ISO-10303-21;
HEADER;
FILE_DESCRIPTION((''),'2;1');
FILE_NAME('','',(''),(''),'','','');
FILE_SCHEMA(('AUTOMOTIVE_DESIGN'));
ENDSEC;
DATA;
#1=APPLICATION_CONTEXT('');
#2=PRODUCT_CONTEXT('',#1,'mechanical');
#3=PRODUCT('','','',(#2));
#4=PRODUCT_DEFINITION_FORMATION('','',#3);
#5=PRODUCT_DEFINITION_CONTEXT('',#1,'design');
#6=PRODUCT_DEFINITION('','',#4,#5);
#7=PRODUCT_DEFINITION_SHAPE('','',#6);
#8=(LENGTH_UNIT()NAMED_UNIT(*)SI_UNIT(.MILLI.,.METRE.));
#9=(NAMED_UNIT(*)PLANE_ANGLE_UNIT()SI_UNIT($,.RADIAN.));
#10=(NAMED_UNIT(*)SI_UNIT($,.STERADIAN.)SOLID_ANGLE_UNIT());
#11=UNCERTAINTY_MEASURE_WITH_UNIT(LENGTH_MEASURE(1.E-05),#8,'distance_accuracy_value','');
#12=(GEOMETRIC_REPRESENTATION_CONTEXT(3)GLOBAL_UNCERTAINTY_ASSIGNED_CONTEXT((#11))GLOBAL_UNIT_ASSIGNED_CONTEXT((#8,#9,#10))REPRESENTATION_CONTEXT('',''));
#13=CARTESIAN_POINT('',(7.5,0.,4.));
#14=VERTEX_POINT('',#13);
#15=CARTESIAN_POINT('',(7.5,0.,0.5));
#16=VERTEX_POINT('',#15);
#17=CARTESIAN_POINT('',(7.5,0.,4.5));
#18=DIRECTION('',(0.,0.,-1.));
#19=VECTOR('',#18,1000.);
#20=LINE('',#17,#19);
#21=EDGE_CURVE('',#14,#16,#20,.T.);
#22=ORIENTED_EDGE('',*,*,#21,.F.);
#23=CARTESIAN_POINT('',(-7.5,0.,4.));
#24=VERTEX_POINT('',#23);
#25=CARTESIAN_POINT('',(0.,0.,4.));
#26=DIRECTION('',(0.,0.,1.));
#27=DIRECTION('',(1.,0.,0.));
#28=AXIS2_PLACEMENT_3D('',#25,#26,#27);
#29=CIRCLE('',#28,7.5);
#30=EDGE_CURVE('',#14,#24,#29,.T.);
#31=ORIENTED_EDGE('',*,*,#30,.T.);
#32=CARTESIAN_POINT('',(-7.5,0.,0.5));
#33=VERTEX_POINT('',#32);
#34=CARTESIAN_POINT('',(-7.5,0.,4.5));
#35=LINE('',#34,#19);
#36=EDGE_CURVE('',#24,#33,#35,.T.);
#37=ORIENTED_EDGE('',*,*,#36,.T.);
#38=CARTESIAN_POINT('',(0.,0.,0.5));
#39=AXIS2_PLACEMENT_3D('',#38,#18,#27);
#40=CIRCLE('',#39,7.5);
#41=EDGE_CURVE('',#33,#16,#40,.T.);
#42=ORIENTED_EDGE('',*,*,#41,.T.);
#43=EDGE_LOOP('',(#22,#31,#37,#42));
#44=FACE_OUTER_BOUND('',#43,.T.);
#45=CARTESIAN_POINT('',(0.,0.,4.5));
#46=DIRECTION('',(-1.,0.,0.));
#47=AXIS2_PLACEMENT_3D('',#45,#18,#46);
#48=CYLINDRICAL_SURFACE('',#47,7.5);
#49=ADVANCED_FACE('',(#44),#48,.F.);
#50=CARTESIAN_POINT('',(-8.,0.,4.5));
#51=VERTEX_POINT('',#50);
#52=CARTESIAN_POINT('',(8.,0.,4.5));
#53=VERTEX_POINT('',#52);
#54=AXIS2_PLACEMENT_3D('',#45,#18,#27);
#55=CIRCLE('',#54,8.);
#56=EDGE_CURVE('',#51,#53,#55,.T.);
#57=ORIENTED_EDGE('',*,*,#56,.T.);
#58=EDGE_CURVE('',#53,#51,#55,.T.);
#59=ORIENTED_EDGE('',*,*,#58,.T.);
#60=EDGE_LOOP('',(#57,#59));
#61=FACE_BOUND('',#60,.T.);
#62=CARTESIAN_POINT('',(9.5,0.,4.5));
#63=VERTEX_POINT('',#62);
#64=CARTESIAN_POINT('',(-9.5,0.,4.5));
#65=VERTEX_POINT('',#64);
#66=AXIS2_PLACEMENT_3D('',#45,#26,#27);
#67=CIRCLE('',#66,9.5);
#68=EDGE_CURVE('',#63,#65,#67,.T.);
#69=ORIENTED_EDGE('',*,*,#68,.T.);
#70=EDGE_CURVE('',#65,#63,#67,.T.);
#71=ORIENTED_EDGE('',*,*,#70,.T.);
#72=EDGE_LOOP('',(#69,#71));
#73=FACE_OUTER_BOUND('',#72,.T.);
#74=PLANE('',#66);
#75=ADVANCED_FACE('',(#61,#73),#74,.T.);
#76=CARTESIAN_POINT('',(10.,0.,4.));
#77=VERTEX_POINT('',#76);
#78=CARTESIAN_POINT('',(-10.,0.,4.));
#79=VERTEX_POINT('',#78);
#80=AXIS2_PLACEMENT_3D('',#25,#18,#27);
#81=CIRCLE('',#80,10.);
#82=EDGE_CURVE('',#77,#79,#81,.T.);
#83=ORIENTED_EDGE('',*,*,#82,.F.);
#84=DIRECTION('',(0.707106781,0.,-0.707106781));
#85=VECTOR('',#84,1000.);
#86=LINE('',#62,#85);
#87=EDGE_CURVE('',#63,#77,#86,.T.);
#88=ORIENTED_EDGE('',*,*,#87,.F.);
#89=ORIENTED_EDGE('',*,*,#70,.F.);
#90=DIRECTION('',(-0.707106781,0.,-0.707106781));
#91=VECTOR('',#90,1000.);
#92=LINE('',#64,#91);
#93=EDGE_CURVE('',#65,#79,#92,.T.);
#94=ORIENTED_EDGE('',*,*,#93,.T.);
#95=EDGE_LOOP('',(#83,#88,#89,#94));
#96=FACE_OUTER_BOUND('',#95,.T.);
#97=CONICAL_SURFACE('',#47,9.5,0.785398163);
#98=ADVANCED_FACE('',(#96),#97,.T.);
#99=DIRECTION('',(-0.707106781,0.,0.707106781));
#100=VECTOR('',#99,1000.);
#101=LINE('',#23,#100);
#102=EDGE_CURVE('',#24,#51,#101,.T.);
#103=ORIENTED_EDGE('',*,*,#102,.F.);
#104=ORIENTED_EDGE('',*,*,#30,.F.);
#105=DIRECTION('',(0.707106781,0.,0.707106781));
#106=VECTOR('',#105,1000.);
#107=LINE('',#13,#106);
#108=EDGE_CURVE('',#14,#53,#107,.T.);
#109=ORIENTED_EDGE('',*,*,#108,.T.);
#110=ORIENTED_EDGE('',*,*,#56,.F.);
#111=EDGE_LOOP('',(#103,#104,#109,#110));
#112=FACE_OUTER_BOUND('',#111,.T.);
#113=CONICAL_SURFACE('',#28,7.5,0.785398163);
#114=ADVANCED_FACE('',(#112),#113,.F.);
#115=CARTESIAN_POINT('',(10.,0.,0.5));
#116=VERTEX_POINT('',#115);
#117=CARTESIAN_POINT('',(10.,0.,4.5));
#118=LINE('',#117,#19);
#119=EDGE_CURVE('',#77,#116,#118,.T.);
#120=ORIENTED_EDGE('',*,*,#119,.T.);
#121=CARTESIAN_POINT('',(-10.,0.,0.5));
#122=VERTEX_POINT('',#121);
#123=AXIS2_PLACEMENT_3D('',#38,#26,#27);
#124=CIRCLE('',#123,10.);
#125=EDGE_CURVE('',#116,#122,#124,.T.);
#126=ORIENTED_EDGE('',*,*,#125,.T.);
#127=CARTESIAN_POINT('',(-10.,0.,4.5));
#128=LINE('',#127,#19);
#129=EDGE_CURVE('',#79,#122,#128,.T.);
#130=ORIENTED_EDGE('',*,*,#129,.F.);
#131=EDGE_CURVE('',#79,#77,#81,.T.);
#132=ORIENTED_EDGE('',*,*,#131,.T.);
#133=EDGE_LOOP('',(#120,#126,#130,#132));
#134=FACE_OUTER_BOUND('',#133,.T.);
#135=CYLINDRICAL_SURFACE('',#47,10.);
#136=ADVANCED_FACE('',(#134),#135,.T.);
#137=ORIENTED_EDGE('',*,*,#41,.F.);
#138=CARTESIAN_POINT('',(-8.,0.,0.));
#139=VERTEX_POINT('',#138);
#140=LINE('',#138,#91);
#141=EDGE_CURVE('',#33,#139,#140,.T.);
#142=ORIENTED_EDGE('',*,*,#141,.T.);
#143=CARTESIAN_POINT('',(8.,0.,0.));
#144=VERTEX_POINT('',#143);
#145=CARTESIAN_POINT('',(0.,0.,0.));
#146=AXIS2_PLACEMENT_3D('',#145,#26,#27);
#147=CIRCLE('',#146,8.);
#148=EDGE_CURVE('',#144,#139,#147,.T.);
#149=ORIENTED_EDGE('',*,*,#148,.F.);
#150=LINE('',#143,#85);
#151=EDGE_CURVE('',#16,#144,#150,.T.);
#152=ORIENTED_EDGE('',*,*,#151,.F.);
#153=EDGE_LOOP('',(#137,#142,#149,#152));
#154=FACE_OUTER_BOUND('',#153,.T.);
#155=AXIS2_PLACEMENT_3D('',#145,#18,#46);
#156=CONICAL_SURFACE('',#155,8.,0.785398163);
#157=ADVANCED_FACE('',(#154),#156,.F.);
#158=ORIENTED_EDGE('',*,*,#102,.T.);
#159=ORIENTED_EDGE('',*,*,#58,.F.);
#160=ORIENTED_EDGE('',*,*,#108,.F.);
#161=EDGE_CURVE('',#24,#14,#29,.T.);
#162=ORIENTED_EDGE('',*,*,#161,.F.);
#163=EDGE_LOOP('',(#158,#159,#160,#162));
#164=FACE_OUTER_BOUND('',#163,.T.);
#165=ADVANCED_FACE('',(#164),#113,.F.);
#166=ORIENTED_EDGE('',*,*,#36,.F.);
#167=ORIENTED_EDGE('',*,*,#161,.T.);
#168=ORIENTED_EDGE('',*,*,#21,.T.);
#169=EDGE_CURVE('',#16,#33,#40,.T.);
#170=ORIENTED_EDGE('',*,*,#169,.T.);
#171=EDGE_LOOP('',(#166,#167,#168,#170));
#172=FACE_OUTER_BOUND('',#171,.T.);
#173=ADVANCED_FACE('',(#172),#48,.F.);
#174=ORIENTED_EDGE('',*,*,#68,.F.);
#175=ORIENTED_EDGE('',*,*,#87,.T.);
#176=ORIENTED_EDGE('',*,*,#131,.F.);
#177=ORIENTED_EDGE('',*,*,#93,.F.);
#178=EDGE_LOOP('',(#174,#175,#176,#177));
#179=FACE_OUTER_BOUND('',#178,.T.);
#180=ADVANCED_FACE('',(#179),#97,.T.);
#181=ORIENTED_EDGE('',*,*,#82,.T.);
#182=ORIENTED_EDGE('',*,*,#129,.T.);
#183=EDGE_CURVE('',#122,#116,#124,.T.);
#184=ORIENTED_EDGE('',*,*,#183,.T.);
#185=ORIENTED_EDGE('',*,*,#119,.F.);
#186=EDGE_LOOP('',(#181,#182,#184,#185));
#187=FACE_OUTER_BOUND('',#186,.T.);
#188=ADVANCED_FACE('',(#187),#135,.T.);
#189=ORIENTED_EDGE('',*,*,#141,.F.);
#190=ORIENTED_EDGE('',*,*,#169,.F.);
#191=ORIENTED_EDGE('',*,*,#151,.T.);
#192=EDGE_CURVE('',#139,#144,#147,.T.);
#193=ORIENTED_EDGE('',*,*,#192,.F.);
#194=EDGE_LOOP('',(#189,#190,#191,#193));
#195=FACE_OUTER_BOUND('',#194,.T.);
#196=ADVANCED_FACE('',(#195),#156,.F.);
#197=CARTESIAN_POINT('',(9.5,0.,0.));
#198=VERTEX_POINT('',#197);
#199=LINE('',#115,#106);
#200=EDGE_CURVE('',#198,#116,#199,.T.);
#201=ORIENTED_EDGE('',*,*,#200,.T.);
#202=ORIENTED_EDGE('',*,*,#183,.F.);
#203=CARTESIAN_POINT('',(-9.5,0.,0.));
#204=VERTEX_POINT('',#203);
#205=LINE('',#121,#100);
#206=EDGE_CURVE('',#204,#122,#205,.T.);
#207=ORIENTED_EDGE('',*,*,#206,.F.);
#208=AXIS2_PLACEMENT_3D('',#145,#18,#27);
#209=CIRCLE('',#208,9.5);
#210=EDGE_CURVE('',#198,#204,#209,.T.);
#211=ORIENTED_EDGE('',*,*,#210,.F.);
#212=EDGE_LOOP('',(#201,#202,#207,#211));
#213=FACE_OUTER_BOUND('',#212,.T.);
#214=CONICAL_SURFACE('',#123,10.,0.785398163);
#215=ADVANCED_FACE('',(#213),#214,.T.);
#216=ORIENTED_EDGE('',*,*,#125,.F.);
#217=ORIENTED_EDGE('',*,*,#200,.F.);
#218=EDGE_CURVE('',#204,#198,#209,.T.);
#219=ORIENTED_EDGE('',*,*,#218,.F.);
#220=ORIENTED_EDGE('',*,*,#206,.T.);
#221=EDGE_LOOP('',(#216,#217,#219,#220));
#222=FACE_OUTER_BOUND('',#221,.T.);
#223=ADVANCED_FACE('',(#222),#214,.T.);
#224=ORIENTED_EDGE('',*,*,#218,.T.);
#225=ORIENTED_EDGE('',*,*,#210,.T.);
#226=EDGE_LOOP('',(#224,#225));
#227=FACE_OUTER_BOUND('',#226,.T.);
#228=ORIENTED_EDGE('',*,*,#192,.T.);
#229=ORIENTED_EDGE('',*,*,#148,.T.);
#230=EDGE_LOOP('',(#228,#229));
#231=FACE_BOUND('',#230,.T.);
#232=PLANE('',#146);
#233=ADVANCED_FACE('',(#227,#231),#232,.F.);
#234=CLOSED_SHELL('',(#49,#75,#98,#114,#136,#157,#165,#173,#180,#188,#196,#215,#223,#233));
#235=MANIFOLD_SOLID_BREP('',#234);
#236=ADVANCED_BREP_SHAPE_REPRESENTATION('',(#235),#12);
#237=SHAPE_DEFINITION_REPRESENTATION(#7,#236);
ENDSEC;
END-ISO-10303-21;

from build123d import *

# Parameters (mm, degrees)
SKETCH1_R           = 10
SKETCH1_R_2         = 7.5
BOSS_EXTRUDE1_DEPTH = 4.5
CHAMFER1_SIZE       = 0.5


with BuildPart() as part:
    # Sketch1 → Boss-Extrude1 (new body)
    with BuildSketch(Plane.XY):
        Circle(SKETCH1_R)
        Circle(SKETCH1_R_2, mode=Mode.SUBTRACT)
    extrude(amount=BOSS_EXTRUDE1_DEPTH)

    # Chamfer1
    chamfer1_edges = [part.edges().sort_by_distance(p)[0] for p in [
        (-10, 0, 0),
        (-10, 0, 4.5),
        (-7.5, 0, 0),
        (-7.5, 0, 4.5),
    ]]
    chamfer(chamfer1_edges, length=CHAMFER1_SIZE)


solid = part.part
